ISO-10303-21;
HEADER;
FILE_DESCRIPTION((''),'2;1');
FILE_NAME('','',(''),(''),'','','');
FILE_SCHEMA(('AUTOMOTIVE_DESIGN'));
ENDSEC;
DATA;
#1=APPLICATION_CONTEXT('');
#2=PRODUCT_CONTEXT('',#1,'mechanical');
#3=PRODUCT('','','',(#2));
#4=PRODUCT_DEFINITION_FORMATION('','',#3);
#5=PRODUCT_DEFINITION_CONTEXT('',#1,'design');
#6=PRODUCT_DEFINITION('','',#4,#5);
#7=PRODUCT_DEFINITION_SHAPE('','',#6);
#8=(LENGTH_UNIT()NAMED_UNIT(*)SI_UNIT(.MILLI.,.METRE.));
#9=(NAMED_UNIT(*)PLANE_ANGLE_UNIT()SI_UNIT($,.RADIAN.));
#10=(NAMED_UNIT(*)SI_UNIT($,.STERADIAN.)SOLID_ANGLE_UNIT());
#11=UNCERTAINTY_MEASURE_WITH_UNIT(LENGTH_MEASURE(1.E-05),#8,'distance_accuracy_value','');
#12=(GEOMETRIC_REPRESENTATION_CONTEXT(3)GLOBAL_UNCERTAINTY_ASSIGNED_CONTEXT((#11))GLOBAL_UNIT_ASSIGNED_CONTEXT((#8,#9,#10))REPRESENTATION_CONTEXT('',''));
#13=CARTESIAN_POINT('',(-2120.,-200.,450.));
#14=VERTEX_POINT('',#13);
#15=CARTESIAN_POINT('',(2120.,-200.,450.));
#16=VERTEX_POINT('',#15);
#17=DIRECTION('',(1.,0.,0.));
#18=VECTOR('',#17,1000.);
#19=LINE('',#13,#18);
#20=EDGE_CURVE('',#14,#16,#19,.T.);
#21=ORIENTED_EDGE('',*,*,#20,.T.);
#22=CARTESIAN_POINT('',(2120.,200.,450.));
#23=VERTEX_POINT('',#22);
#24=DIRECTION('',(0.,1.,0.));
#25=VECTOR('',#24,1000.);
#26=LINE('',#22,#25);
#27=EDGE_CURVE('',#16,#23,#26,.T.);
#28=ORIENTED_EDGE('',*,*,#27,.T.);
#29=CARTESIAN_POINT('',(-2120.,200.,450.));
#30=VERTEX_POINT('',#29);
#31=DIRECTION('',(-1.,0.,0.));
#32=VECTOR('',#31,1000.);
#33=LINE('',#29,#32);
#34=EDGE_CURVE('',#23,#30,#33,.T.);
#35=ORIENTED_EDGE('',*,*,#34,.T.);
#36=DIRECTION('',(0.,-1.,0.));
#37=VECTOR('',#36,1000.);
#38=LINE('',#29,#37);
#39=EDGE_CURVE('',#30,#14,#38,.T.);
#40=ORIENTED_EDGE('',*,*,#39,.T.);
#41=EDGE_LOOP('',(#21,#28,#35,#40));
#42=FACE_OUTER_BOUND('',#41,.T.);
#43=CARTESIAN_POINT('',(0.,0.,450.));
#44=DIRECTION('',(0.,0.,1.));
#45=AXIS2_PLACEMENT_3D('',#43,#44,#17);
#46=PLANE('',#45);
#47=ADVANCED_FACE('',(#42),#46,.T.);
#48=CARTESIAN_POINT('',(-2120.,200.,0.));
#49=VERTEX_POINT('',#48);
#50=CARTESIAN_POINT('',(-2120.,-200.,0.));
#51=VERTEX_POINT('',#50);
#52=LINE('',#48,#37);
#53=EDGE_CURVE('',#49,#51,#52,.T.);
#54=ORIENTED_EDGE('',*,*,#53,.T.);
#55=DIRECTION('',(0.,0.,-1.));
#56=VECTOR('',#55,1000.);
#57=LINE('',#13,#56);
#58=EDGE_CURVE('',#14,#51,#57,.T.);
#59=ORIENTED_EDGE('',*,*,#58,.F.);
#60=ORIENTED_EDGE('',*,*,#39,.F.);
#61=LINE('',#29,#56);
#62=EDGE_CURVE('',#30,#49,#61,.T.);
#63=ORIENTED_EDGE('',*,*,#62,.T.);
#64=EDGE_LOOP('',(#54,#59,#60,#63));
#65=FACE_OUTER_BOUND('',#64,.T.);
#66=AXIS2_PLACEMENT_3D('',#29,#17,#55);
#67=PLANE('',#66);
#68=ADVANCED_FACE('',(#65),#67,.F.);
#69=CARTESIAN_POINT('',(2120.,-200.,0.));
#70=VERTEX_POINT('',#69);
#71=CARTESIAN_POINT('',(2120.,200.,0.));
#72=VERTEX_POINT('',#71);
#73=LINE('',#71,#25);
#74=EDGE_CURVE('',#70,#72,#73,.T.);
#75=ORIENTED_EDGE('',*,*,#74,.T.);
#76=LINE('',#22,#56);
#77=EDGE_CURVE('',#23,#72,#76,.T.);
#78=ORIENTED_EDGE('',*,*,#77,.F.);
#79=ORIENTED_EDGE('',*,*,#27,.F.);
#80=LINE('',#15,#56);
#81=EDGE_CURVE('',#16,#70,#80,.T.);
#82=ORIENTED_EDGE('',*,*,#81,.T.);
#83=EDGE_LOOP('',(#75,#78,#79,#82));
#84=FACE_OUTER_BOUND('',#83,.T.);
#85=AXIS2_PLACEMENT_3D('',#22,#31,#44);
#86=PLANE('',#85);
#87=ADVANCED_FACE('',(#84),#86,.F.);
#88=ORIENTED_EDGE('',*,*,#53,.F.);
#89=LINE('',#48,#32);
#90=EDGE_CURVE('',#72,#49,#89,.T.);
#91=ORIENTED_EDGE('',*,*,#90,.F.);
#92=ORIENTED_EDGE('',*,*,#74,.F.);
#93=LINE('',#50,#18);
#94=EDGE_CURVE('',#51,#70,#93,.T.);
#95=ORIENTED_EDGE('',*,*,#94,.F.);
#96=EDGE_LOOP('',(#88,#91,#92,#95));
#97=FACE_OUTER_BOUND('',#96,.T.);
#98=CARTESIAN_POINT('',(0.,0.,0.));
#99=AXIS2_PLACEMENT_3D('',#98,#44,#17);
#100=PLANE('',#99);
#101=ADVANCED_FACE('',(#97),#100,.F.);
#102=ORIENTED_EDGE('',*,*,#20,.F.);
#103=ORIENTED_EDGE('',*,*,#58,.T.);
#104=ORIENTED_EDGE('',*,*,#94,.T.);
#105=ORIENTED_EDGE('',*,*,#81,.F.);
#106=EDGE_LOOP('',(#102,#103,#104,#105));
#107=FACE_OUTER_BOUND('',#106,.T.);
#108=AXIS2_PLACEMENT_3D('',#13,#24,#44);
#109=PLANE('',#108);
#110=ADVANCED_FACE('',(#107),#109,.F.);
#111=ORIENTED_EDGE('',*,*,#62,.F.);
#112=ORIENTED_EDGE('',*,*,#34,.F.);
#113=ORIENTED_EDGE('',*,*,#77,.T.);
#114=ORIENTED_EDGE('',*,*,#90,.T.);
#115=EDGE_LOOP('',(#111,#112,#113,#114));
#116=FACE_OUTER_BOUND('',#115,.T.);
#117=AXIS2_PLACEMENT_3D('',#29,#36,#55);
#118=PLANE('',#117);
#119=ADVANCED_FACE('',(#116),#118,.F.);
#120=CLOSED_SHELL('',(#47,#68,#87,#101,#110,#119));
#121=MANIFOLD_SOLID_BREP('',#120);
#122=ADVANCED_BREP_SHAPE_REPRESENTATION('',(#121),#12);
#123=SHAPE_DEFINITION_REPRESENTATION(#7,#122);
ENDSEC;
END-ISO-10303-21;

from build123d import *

# Parameters (mm, degrees)
SKETCH_1_W      = 4240
SKETCH_1_H      = 400
EXTRUDE_1_DEPTH = 450


with BuildPart() as part:
    # 草图1 → 凸台-拉伸1 (new body)
    with BuildSketch(Plane.XY):
        Rectangle(SKETCH_1_W, SKETCH_1_H)
    extrude(amount=EXTRUDE_1_DEPTH)


solid = part.part
